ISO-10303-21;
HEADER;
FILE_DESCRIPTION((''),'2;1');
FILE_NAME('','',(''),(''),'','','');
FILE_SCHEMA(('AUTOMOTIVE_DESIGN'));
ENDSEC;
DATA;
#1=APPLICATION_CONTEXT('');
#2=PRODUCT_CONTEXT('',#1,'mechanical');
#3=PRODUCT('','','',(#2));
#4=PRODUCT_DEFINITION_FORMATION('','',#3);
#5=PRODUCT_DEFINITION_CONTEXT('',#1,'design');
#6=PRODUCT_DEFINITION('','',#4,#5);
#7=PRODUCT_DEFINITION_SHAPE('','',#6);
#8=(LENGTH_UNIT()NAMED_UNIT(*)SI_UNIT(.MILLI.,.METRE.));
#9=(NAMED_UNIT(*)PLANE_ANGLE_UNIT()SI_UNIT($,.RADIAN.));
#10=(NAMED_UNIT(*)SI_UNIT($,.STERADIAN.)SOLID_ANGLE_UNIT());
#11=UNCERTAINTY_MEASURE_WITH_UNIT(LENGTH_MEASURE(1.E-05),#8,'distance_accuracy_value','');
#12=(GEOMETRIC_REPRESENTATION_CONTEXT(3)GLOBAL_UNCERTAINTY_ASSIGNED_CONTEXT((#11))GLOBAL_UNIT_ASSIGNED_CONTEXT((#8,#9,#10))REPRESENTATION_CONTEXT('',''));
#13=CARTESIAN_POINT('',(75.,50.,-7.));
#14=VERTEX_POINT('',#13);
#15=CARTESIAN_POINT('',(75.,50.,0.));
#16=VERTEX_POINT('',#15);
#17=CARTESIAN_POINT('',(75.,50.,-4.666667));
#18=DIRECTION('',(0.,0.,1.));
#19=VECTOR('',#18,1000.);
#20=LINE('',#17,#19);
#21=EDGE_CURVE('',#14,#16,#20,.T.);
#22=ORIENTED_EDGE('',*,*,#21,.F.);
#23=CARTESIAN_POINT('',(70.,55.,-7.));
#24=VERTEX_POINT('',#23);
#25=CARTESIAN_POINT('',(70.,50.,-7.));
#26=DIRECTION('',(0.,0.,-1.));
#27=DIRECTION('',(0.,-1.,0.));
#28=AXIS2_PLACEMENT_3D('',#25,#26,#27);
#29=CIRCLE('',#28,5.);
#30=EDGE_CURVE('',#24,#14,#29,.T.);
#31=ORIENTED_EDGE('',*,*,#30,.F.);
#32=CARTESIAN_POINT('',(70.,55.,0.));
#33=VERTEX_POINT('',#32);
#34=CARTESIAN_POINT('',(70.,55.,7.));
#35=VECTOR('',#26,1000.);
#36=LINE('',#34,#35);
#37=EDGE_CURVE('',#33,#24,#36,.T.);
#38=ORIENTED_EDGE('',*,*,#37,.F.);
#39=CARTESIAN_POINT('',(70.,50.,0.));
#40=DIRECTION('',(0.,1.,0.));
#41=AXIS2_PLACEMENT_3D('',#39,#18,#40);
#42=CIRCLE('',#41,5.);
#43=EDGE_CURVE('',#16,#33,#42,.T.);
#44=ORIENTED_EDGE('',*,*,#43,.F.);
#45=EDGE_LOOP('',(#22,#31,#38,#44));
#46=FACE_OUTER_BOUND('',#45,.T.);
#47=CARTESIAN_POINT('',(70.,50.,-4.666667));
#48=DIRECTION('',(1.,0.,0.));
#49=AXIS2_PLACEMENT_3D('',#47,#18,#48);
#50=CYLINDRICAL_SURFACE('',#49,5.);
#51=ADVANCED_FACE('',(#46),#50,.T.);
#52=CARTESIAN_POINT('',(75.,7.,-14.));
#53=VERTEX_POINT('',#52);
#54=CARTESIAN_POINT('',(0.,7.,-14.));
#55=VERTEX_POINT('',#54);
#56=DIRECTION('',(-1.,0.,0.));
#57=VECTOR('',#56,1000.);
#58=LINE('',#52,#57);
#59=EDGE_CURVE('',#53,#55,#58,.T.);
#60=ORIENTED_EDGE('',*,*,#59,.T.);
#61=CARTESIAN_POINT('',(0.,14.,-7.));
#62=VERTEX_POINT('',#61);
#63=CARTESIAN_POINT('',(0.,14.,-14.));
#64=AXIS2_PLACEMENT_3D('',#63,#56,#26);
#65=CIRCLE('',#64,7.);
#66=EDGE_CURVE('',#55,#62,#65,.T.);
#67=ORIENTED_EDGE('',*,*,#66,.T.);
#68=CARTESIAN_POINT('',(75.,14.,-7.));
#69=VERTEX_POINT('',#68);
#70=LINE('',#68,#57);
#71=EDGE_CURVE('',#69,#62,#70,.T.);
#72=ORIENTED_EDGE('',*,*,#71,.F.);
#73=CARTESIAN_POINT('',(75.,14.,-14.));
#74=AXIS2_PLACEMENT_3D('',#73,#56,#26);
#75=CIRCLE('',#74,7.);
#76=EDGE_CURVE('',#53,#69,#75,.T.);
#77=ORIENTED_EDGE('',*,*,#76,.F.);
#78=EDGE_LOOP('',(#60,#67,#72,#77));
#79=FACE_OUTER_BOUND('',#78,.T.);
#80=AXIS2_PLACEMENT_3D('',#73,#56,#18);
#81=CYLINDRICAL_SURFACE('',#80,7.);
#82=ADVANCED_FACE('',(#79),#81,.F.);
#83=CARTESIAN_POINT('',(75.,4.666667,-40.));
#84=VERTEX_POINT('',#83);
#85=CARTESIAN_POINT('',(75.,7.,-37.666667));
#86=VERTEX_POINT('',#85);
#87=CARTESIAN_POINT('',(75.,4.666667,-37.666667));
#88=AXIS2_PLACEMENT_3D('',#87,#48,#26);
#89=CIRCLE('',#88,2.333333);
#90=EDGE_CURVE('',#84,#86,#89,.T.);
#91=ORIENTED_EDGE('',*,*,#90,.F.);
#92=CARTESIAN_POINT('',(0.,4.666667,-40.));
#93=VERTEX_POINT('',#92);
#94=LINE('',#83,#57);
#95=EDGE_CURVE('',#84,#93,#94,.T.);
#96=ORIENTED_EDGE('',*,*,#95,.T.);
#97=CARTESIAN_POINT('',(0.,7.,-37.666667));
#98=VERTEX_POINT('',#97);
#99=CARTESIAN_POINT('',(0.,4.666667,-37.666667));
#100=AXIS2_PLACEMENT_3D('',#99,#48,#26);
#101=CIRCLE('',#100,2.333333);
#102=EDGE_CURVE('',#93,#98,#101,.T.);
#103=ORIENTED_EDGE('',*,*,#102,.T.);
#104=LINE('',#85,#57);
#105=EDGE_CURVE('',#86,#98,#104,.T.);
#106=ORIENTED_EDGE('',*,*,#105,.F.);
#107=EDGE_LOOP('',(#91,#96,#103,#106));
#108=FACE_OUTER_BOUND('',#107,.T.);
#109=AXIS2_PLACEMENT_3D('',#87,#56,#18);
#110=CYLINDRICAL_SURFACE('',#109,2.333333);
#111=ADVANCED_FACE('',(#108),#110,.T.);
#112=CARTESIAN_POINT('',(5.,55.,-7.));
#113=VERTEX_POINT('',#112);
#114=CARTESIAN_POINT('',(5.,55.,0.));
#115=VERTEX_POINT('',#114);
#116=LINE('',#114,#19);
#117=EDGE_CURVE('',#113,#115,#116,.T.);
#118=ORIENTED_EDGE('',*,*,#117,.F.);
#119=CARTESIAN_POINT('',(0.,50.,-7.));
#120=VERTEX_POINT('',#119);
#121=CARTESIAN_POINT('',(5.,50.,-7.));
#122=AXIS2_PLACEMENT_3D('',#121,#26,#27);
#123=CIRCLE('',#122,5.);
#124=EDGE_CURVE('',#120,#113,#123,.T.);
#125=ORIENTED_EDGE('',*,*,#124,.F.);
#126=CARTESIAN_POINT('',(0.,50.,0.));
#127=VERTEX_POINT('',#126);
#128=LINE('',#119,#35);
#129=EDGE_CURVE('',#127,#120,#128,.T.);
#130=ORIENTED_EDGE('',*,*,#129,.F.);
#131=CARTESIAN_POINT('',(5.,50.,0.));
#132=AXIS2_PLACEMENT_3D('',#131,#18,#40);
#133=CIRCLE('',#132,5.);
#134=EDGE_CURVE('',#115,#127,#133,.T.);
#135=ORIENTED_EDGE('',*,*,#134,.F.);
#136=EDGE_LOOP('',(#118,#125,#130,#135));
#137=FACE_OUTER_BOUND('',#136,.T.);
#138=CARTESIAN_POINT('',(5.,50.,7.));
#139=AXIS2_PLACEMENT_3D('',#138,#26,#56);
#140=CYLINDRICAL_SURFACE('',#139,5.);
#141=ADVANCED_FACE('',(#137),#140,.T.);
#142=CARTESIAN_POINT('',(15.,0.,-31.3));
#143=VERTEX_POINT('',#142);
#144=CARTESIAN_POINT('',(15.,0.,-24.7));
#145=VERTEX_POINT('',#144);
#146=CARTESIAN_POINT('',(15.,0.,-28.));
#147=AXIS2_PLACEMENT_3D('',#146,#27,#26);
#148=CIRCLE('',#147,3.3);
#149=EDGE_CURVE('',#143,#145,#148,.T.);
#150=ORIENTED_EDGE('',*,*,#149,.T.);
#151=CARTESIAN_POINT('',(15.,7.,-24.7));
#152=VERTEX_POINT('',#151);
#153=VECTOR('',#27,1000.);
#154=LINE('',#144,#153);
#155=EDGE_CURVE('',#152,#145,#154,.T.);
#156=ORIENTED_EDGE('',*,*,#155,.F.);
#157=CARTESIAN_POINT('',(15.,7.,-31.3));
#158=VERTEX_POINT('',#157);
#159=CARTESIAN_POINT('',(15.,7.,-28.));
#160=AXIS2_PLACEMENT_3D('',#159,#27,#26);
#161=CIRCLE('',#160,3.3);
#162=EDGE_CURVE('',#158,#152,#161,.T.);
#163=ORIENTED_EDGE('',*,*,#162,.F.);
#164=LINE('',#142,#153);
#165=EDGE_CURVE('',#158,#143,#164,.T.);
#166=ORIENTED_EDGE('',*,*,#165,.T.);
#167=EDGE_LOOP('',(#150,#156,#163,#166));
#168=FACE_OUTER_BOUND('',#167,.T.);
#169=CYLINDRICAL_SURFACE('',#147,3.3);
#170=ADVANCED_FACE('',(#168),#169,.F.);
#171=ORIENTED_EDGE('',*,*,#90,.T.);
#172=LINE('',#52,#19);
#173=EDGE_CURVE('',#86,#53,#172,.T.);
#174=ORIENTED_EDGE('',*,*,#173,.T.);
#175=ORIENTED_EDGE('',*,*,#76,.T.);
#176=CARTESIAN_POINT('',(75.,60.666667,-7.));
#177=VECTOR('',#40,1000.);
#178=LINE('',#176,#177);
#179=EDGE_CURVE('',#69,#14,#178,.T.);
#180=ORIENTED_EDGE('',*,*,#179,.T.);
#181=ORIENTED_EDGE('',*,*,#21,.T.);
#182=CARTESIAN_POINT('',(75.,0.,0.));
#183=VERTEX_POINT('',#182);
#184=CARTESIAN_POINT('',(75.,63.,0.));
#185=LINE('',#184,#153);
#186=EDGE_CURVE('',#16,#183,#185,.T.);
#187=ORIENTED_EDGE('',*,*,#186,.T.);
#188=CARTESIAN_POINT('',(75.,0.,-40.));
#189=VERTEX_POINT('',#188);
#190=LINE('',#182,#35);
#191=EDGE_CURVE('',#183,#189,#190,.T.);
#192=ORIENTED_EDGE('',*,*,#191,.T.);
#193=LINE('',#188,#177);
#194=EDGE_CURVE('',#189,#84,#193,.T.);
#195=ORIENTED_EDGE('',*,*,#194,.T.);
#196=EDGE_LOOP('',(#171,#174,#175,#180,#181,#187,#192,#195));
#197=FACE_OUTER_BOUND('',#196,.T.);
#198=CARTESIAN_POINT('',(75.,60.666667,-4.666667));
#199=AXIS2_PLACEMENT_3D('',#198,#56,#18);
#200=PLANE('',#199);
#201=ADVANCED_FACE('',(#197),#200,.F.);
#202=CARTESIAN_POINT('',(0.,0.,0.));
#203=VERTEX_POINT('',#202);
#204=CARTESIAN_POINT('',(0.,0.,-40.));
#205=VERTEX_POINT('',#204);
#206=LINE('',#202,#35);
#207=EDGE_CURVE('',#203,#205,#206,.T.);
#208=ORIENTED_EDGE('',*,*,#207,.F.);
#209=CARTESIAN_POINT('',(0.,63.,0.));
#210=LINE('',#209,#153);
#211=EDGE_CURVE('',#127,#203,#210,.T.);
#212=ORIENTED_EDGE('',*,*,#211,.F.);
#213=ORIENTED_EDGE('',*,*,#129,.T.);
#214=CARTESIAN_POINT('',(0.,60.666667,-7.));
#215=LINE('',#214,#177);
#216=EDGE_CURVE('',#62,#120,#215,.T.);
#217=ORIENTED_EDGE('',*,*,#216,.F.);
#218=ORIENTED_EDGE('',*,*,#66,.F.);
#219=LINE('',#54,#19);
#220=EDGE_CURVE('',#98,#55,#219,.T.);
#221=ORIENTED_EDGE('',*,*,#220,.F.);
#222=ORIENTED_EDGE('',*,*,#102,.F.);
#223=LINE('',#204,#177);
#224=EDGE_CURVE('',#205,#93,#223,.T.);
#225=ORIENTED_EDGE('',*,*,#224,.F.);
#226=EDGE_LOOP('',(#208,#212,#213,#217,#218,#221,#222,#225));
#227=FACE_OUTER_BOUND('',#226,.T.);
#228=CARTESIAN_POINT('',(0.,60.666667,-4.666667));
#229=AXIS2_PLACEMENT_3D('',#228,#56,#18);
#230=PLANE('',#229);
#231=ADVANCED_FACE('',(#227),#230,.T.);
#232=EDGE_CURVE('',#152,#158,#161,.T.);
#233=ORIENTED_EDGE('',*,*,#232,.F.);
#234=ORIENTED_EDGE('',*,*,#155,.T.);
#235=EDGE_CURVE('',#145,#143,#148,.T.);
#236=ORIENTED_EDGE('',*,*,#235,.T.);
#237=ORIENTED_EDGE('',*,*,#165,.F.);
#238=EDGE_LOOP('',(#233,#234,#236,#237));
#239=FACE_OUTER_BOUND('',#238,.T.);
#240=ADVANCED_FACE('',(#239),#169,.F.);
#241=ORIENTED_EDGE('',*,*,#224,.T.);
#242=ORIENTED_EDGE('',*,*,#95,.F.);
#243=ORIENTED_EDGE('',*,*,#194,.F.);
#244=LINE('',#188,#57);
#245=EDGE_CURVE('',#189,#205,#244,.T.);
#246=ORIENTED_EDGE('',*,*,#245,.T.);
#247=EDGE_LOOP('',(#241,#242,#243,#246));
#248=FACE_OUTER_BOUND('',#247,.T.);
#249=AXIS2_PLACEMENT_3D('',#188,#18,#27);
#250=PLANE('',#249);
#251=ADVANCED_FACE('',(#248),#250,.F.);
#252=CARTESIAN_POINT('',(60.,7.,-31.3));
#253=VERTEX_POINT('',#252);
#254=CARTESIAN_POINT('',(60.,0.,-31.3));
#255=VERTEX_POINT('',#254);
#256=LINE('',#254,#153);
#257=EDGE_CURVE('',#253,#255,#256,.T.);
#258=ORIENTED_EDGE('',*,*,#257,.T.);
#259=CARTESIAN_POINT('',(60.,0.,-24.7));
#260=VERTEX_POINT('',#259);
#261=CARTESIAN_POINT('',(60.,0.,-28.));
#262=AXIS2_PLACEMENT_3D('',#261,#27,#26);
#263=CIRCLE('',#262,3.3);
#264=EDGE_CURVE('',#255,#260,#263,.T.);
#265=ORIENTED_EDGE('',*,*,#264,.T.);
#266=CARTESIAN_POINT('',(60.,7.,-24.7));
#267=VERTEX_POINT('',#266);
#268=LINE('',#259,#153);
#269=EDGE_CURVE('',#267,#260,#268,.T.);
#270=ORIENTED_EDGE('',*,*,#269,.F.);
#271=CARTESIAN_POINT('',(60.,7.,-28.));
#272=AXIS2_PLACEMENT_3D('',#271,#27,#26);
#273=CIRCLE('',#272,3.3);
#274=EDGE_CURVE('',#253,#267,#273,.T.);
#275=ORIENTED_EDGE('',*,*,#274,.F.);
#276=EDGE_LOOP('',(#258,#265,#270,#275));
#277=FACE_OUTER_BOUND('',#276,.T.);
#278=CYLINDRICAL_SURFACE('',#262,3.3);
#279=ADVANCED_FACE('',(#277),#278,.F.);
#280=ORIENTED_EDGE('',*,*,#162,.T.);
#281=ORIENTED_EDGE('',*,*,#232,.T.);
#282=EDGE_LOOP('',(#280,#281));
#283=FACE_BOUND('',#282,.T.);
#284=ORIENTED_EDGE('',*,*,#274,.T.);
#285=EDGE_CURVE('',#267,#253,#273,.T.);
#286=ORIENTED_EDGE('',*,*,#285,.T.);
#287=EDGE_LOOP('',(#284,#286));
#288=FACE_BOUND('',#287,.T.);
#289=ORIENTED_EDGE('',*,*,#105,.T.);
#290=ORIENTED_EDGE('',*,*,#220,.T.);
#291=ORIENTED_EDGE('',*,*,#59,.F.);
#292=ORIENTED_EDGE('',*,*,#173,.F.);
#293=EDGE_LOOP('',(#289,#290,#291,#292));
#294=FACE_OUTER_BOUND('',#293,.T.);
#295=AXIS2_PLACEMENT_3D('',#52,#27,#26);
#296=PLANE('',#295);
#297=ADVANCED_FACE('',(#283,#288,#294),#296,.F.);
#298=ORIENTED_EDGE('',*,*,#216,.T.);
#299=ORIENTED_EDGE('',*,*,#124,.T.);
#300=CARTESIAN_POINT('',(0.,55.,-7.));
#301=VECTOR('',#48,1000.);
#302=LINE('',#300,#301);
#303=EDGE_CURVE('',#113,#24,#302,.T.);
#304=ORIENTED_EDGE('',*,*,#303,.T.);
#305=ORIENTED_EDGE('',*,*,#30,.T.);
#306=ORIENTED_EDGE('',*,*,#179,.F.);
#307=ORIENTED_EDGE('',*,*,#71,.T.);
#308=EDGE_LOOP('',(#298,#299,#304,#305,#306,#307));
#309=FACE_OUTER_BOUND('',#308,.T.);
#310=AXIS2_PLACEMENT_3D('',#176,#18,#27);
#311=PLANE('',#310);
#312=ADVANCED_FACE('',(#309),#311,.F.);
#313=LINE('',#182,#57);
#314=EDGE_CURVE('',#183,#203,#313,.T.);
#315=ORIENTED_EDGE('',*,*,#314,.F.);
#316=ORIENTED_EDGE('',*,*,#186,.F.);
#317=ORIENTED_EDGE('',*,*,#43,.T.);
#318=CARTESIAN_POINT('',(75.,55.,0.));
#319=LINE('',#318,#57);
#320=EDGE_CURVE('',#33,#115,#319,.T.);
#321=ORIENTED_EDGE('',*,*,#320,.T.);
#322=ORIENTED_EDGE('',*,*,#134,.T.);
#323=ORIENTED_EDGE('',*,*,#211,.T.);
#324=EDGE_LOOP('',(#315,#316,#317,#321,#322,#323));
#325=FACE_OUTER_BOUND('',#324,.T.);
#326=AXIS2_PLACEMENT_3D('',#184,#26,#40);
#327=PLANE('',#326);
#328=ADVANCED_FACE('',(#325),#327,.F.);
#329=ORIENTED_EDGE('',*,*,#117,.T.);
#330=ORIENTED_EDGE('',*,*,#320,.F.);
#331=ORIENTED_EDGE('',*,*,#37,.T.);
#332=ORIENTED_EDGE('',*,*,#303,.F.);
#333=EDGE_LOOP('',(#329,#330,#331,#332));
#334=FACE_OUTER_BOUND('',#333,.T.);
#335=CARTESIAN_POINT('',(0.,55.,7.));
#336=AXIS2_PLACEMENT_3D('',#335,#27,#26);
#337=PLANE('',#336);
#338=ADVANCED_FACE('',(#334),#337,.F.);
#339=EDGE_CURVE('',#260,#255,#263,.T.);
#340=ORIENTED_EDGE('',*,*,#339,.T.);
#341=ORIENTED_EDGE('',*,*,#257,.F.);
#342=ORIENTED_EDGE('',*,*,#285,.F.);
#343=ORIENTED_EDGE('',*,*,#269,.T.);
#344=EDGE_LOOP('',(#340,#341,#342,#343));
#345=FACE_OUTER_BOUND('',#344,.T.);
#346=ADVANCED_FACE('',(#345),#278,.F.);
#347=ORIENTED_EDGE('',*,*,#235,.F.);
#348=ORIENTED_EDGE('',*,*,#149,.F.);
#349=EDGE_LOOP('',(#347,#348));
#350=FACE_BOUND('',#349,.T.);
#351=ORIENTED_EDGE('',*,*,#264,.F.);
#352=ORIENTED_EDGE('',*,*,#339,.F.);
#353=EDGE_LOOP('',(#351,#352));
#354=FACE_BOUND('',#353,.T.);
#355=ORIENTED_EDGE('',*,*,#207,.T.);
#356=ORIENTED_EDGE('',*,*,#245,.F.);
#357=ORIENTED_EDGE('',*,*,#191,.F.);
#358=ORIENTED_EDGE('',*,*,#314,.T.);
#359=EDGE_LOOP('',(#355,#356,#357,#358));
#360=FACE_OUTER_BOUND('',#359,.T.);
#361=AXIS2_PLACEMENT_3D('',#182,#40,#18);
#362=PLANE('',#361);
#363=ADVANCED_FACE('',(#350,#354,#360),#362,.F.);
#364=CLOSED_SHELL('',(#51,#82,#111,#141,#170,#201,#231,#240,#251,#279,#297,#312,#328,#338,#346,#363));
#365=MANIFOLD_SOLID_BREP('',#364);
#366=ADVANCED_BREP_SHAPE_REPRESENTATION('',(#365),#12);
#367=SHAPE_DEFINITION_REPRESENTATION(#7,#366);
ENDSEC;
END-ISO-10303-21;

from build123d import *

# Parameters (mm, degrees)
UNEQUAL_ANGLE_6_3_4_1_DEPTH = 75
M6_CLEARANCE_HOLE1_D        = 6.6
M6_CLEARANCE_HOLE1_DEPTH    = 20
M6_CLEARANCE_HOLE1_TIP      = 1.982840043
CUT_EXTRUDE1_DEPTH          = 106.80170131
CUT_EXTRUDE1_DEPTH_BACK     = 106.80170131
SKETCH8_W                   = 14
SKETCH8_H                   = 16
FILLET1_R                   = 5


with BuildPart() as part:
    # Sketch11 → Unequal angle 6.3-4(1) (new body)
    with BuildSketch(Plane.YZ):
        with BuildLine():
            Line((63, 0), (0, 0))
            Line((0, 0), (0, -40))
            Line((0, -40), (4.666666667, -40))
            ThreePointArc((4.666666667, -40), (6.316582489, -39.316582489), (7, -37.666666667))
            Line((7, -37.666666667), (7, -14))
            ThreePointArc((7, -14), (9.050252532, -9.050252532), (14, -7))
            Line((14, -7), (60.666666667, -7))
            ThreePointArc((60.666666667, -7), (62.316582489, -6.316582489), (63, -4.666666667))
            Line((63, -4.666666667), (63, 0))
        make_face()
    extrude(amount=UNEQUAL_ANGLE_6_3_4_1_DEPTH)

    # M6 Clearance Hole1
    with Locations(Plane.XZ):
        with Locations((15, -28), (60, -28)):
            Hole(M6_CLEARANCE_HOLE1_D / 2, depth=M6_CLEARANCE_HOLE1_DEPTH)
            with Locations((0, 0, -(M6_CLEARANCE_HOLE1_DEPTH + M6_CLEARANCE_HOLE1_TIP / 2))):  # 118° drill point
                Cone(0, M6_CLEARANCE_HOLE1_D / 2, M6_CLEARANCE_HOLE1_TIP, mode=Mode.SUBTRACT)

    # Sketch8 → Cut-Extrude1 (cut, two sides: drawn at the far end of the back side and taken through both)
    with BuildSketch(Plane(origin=(75, 0, 0), x_dir=(0, 0, -1), z_dir=(1, 0, 0)).offset(-CUT_EXTRUDE1_DEPTH_BACK)):
        with Locations((0, 63)):
            Rectangle(SKETCH8_W, SKETCH8_H)
    extrude(amount=CUT_EXTRUDE1_DEPTH + CUT_EXTRUDE1_DEPTH_BACK, mode=Mode.SUBTRACT)

    # Fillet1
    fillet1_edges = [part.edges().sort_by_distance(p)[0] for p in [
        (0, 55, -3.5),
        (75, 55, -3.5),
    ]]
    fillet(fillet1_edges, radius=FILLET1_R)


solid = part.part
